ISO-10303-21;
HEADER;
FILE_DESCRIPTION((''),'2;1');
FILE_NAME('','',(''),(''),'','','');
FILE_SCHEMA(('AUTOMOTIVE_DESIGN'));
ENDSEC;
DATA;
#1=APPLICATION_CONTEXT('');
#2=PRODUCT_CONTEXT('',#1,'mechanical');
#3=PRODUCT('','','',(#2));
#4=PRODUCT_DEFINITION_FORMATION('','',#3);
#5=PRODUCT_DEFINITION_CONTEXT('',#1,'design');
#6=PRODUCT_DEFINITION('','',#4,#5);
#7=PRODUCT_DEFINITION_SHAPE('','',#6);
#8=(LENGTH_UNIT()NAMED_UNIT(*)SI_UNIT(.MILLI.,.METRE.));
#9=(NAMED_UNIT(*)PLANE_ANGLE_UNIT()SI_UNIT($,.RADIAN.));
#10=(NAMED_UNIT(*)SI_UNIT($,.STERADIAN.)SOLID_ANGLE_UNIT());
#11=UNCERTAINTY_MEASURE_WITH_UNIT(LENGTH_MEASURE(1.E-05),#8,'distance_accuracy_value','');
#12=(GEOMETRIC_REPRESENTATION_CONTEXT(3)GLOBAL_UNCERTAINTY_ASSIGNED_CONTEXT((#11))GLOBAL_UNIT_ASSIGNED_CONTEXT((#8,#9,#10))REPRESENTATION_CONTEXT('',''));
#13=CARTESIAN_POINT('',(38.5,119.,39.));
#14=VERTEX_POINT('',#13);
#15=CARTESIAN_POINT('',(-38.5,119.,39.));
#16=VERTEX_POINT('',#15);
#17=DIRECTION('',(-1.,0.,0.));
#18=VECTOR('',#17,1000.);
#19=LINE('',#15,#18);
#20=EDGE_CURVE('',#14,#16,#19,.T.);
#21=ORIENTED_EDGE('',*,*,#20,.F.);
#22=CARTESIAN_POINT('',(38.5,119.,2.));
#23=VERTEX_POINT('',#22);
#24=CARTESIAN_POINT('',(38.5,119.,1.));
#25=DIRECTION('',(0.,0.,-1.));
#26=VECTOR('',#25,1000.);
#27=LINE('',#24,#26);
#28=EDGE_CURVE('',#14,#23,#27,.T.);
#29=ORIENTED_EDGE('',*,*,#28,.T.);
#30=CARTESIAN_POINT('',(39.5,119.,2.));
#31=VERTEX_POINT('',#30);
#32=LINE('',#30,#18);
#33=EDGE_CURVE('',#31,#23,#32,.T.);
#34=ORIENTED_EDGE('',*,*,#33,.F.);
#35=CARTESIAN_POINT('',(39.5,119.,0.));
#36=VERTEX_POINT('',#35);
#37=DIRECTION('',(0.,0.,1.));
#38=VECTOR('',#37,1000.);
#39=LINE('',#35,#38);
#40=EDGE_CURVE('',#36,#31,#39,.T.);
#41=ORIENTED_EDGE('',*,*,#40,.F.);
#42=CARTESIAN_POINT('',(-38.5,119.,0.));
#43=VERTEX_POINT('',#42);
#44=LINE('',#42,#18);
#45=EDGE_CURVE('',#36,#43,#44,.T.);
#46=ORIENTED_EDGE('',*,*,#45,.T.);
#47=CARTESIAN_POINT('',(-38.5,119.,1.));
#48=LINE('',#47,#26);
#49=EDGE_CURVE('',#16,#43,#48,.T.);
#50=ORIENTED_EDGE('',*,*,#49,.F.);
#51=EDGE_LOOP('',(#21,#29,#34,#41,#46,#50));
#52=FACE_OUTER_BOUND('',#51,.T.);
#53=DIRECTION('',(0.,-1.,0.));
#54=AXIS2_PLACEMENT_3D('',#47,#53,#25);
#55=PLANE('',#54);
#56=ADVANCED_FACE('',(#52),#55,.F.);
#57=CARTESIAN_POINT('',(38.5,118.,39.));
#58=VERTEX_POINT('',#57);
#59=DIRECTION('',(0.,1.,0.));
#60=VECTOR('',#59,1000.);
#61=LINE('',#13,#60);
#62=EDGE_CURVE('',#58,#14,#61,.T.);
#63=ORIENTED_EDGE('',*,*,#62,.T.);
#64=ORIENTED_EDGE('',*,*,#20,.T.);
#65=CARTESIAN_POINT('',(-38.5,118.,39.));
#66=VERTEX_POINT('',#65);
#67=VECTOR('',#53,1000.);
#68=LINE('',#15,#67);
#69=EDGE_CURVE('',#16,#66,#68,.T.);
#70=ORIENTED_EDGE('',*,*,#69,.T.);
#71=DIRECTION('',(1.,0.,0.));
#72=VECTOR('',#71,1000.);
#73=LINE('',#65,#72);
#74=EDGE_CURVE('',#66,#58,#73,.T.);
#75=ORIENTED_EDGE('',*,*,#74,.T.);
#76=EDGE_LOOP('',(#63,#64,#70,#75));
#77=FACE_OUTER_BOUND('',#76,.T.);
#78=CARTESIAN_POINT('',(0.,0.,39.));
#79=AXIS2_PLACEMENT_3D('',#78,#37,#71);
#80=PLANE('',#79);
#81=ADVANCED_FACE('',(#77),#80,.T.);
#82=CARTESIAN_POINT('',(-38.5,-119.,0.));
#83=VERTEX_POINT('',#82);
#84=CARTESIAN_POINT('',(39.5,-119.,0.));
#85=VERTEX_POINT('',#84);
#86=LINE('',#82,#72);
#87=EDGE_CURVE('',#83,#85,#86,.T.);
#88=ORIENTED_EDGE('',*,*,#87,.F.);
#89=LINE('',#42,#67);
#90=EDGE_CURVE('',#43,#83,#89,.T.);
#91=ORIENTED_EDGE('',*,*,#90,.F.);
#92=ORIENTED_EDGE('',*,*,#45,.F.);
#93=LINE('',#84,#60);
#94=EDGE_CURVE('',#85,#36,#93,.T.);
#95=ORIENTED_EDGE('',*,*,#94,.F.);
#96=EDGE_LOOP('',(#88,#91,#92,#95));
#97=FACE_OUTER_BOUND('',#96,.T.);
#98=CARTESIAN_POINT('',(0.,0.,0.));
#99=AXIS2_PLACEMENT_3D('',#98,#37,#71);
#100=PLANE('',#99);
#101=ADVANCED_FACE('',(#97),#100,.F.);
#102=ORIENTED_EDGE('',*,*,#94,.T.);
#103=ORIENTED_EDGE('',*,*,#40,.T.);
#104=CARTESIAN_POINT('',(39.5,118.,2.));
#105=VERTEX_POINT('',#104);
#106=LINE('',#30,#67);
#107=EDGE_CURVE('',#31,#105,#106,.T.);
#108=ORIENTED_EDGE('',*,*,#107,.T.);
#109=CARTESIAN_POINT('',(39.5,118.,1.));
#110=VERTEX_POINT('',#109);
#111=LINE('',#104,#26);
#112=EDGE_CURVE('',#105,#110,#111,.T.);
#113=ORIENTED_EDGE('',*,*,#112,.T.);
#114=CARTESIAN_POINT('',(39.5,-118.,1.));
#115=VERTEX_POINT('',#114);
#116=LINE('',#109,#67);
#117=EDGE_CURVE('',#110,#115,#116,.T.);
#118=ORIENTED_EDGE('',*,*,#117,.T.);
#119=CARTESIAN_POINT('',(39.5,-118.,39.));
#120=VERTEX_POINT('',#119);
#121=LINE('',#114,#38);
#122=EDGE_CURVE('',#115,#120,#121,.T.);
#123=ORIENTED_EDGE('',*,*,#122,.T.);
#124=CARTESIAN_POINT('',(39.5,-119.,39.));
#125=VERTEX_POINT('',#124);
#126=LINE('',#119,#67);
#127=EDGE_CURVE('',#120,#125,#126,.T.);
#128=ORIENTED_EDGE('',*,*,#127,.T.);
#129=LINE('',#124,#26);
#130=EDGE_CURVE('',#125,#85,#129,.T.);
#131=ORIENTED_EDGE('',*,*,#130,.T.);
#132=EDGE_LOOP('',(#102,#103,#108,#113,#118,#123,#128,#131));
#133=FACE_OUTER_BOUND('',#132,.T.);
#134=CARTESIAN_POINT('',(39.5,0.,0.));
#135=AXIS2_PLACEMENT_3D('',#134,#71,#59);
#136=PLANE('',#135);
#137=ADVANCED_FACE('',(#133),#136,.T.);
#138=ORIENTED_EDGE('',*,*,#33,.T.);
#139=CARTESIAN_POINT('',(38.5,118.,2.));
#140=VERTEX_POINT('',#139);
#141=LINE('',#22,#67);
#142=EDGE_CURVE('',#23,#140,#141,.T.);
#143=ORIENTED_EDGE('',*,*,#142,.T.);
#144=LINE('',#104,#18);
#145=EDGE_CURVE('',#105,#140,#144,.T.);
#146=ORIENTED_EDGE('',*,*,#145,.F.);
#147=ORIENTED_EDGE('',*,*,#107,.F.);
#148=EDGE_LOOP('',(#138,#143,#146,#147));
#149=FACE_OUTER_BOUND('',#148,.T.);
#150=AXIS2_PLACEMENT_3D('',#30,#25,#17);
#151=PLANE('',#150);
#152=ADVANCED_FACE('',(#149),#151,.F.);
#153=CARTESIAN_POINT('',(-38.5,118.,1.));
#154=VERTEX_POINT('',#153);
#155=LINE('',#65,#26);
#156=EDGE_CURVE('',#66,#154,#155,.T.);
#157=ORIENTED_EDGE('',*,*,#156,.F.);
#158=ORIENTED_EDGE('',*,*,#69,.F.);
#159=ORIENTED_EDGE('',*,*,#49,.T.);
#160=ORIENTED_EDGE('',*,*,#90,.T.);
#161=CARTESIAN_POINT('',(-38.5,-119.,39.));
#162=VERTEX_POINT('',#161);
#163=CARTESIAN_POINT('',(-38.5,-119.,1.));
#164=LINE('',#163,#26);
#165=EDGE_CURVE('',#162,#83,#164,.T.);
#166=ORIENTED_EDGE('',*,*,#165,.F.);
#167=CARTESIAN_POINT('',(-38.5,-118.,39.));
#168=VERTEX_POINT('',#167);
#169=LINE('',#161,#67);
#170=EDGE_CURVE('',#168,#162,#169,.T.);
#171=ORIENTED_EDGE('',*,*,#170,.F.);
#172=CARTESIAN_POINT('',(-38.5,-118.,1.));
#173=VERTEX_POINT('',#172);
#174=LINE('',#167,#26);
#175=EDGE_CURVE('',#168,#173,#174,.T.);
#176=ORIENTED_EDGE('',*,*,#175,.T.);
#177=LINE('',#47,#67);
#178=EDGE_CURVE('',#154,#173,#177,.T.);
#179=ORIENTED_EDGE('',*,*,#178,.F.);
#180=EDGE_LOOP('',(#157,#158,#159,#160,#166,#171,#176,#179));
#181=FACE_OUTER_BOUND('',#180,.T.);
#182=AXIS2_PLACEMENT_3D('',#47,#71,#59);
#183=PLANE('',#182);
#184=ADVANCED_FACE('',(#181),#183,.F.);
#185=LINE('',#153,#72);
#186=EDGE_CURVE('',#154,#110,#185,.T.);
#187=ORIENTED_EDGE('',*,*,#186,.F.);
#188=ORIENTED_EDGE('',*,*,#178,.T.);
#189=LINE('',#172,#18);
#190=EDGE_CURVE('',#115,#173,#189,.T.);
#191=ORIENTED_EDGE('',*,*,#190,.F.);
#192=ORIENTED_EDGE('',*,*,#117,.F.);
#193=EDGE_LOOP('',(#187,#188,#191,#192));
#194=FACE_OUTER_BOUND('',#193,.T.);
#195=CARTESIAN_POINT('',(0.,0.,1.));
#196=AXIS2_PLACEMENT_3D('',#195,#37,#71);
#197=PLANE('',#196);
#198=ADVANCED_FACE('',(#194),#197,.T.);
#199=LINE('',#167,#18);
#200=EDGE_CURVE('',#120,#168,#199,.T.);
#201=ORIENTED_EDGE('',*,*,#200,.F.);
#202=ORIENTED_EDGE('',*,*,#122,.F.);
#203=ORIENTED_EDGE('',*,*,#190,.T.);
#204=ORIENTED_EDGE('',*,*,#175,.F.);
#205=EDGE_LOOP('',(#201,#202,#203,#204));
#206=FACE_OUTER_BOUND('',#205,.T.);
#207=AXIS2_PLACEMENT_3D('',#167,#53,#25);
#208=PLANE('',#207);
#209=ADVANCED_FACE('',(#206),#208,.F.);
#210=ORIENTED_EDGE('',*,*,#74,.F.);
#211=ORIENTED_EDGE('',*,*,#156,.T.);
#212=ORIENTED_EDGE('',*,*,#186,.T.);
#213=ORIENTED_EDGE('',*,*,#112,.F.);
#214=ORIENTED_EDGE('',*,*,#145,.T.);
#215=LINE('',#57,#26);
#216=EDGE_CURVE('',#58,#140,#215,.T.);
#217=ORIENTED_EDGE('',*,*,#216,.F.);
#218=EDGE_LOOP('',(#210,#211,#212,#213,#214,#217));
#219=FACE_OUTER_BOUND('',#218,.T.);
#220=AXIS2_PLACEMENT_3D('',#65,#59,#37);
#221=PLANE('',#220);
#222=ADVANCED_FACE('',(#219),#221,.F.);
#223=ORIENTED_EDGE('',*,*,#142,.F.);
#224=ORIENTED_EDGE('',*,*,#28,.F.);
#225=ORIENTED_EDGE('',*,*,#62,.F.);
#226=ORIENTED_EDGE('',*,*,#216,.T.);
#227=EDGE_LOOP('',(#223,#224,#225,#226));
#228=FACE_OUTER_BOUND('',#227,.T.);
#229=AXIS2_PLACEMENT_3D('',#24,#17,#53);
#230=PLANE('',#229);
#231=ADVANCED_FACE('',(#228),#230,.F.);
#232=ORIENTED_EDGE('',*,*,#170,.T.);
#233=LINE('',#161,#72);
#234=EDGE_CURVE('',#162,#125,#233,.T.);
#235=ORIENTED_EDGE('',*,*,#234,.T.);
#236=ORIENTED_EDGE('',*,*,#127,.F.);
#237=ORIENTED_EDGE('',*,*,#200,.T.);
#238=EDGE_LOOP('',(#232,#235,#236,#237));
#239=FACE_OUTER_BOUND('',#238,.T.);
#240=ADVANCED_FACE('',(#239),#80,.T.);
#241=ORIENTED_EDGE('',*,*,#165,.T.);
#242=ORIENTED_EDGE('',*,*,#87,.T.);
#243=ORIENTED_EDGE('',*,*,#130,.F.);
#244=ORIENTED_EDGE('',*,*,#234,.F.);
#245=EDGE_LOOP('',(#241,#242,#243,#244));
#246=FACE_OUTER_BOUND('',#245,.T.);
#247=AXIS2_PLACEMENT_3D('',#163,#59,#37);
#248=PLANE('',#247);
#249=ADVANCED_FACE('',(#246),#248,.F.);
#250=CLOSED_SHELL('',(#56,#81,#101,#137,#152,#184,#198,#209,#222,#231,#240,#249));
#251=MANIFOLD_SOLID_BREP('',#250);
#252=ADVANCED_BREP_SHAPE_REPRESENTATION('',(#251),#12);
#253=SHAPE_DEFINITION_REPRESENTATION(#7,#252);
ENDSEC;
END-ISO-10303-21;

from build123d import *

# Parameters (mm, degrees)
SKETCH1_W           = 77
SKETCH1_H           = 238
BOSS_EXTRUDE1_DEPTH = 1
SKETCH2_W           = 77
SKETCH2_H           = 1
BOSS_EXTRUDE2_DEPTH = 38
BOSS_EXTRUDE3_DEPTH = 1


with BuildPart() as part:
    # Sketch1 → Boss-Extrude1 (new body)
    with BuildSketch(Plane.XY):
        Rectangle(SKETCH1_W, SKETCH1_H)
    extrude(amount=BOSS_EXTRUDE1_DEPTH)

    # Sketch2 → Boss-Extrude2 (add)
    with BuildSketch(Plane.XY.offset(1)):
        with Locations((0, 118.5)):
            Rectangle(SKETCH2_W, SKETCH2_H)
        with Locations((0, -118.5)):
            Rectangle(SKETCH2_W, SKETCH2_H)
    extrude(amount=BOSS_EXTRUDE2_DEPTH)

    # Sketch3 → Boss-Extrude3 (add)
    with BuildSketch(Plane(origin=(38.5, 0, 0), x_dir=(0, 0, -1), z_dir=(1, 0, 0))):
        Polygon((-2, 119), (-2, 118), (-1, 118), (-1, -118), (-39, -118), (-39, -119), (0, -119), (0, 119), align=None)
    extrude(amount=BOSS_EXTRUDE3_DEPTH)


solid = part.part
